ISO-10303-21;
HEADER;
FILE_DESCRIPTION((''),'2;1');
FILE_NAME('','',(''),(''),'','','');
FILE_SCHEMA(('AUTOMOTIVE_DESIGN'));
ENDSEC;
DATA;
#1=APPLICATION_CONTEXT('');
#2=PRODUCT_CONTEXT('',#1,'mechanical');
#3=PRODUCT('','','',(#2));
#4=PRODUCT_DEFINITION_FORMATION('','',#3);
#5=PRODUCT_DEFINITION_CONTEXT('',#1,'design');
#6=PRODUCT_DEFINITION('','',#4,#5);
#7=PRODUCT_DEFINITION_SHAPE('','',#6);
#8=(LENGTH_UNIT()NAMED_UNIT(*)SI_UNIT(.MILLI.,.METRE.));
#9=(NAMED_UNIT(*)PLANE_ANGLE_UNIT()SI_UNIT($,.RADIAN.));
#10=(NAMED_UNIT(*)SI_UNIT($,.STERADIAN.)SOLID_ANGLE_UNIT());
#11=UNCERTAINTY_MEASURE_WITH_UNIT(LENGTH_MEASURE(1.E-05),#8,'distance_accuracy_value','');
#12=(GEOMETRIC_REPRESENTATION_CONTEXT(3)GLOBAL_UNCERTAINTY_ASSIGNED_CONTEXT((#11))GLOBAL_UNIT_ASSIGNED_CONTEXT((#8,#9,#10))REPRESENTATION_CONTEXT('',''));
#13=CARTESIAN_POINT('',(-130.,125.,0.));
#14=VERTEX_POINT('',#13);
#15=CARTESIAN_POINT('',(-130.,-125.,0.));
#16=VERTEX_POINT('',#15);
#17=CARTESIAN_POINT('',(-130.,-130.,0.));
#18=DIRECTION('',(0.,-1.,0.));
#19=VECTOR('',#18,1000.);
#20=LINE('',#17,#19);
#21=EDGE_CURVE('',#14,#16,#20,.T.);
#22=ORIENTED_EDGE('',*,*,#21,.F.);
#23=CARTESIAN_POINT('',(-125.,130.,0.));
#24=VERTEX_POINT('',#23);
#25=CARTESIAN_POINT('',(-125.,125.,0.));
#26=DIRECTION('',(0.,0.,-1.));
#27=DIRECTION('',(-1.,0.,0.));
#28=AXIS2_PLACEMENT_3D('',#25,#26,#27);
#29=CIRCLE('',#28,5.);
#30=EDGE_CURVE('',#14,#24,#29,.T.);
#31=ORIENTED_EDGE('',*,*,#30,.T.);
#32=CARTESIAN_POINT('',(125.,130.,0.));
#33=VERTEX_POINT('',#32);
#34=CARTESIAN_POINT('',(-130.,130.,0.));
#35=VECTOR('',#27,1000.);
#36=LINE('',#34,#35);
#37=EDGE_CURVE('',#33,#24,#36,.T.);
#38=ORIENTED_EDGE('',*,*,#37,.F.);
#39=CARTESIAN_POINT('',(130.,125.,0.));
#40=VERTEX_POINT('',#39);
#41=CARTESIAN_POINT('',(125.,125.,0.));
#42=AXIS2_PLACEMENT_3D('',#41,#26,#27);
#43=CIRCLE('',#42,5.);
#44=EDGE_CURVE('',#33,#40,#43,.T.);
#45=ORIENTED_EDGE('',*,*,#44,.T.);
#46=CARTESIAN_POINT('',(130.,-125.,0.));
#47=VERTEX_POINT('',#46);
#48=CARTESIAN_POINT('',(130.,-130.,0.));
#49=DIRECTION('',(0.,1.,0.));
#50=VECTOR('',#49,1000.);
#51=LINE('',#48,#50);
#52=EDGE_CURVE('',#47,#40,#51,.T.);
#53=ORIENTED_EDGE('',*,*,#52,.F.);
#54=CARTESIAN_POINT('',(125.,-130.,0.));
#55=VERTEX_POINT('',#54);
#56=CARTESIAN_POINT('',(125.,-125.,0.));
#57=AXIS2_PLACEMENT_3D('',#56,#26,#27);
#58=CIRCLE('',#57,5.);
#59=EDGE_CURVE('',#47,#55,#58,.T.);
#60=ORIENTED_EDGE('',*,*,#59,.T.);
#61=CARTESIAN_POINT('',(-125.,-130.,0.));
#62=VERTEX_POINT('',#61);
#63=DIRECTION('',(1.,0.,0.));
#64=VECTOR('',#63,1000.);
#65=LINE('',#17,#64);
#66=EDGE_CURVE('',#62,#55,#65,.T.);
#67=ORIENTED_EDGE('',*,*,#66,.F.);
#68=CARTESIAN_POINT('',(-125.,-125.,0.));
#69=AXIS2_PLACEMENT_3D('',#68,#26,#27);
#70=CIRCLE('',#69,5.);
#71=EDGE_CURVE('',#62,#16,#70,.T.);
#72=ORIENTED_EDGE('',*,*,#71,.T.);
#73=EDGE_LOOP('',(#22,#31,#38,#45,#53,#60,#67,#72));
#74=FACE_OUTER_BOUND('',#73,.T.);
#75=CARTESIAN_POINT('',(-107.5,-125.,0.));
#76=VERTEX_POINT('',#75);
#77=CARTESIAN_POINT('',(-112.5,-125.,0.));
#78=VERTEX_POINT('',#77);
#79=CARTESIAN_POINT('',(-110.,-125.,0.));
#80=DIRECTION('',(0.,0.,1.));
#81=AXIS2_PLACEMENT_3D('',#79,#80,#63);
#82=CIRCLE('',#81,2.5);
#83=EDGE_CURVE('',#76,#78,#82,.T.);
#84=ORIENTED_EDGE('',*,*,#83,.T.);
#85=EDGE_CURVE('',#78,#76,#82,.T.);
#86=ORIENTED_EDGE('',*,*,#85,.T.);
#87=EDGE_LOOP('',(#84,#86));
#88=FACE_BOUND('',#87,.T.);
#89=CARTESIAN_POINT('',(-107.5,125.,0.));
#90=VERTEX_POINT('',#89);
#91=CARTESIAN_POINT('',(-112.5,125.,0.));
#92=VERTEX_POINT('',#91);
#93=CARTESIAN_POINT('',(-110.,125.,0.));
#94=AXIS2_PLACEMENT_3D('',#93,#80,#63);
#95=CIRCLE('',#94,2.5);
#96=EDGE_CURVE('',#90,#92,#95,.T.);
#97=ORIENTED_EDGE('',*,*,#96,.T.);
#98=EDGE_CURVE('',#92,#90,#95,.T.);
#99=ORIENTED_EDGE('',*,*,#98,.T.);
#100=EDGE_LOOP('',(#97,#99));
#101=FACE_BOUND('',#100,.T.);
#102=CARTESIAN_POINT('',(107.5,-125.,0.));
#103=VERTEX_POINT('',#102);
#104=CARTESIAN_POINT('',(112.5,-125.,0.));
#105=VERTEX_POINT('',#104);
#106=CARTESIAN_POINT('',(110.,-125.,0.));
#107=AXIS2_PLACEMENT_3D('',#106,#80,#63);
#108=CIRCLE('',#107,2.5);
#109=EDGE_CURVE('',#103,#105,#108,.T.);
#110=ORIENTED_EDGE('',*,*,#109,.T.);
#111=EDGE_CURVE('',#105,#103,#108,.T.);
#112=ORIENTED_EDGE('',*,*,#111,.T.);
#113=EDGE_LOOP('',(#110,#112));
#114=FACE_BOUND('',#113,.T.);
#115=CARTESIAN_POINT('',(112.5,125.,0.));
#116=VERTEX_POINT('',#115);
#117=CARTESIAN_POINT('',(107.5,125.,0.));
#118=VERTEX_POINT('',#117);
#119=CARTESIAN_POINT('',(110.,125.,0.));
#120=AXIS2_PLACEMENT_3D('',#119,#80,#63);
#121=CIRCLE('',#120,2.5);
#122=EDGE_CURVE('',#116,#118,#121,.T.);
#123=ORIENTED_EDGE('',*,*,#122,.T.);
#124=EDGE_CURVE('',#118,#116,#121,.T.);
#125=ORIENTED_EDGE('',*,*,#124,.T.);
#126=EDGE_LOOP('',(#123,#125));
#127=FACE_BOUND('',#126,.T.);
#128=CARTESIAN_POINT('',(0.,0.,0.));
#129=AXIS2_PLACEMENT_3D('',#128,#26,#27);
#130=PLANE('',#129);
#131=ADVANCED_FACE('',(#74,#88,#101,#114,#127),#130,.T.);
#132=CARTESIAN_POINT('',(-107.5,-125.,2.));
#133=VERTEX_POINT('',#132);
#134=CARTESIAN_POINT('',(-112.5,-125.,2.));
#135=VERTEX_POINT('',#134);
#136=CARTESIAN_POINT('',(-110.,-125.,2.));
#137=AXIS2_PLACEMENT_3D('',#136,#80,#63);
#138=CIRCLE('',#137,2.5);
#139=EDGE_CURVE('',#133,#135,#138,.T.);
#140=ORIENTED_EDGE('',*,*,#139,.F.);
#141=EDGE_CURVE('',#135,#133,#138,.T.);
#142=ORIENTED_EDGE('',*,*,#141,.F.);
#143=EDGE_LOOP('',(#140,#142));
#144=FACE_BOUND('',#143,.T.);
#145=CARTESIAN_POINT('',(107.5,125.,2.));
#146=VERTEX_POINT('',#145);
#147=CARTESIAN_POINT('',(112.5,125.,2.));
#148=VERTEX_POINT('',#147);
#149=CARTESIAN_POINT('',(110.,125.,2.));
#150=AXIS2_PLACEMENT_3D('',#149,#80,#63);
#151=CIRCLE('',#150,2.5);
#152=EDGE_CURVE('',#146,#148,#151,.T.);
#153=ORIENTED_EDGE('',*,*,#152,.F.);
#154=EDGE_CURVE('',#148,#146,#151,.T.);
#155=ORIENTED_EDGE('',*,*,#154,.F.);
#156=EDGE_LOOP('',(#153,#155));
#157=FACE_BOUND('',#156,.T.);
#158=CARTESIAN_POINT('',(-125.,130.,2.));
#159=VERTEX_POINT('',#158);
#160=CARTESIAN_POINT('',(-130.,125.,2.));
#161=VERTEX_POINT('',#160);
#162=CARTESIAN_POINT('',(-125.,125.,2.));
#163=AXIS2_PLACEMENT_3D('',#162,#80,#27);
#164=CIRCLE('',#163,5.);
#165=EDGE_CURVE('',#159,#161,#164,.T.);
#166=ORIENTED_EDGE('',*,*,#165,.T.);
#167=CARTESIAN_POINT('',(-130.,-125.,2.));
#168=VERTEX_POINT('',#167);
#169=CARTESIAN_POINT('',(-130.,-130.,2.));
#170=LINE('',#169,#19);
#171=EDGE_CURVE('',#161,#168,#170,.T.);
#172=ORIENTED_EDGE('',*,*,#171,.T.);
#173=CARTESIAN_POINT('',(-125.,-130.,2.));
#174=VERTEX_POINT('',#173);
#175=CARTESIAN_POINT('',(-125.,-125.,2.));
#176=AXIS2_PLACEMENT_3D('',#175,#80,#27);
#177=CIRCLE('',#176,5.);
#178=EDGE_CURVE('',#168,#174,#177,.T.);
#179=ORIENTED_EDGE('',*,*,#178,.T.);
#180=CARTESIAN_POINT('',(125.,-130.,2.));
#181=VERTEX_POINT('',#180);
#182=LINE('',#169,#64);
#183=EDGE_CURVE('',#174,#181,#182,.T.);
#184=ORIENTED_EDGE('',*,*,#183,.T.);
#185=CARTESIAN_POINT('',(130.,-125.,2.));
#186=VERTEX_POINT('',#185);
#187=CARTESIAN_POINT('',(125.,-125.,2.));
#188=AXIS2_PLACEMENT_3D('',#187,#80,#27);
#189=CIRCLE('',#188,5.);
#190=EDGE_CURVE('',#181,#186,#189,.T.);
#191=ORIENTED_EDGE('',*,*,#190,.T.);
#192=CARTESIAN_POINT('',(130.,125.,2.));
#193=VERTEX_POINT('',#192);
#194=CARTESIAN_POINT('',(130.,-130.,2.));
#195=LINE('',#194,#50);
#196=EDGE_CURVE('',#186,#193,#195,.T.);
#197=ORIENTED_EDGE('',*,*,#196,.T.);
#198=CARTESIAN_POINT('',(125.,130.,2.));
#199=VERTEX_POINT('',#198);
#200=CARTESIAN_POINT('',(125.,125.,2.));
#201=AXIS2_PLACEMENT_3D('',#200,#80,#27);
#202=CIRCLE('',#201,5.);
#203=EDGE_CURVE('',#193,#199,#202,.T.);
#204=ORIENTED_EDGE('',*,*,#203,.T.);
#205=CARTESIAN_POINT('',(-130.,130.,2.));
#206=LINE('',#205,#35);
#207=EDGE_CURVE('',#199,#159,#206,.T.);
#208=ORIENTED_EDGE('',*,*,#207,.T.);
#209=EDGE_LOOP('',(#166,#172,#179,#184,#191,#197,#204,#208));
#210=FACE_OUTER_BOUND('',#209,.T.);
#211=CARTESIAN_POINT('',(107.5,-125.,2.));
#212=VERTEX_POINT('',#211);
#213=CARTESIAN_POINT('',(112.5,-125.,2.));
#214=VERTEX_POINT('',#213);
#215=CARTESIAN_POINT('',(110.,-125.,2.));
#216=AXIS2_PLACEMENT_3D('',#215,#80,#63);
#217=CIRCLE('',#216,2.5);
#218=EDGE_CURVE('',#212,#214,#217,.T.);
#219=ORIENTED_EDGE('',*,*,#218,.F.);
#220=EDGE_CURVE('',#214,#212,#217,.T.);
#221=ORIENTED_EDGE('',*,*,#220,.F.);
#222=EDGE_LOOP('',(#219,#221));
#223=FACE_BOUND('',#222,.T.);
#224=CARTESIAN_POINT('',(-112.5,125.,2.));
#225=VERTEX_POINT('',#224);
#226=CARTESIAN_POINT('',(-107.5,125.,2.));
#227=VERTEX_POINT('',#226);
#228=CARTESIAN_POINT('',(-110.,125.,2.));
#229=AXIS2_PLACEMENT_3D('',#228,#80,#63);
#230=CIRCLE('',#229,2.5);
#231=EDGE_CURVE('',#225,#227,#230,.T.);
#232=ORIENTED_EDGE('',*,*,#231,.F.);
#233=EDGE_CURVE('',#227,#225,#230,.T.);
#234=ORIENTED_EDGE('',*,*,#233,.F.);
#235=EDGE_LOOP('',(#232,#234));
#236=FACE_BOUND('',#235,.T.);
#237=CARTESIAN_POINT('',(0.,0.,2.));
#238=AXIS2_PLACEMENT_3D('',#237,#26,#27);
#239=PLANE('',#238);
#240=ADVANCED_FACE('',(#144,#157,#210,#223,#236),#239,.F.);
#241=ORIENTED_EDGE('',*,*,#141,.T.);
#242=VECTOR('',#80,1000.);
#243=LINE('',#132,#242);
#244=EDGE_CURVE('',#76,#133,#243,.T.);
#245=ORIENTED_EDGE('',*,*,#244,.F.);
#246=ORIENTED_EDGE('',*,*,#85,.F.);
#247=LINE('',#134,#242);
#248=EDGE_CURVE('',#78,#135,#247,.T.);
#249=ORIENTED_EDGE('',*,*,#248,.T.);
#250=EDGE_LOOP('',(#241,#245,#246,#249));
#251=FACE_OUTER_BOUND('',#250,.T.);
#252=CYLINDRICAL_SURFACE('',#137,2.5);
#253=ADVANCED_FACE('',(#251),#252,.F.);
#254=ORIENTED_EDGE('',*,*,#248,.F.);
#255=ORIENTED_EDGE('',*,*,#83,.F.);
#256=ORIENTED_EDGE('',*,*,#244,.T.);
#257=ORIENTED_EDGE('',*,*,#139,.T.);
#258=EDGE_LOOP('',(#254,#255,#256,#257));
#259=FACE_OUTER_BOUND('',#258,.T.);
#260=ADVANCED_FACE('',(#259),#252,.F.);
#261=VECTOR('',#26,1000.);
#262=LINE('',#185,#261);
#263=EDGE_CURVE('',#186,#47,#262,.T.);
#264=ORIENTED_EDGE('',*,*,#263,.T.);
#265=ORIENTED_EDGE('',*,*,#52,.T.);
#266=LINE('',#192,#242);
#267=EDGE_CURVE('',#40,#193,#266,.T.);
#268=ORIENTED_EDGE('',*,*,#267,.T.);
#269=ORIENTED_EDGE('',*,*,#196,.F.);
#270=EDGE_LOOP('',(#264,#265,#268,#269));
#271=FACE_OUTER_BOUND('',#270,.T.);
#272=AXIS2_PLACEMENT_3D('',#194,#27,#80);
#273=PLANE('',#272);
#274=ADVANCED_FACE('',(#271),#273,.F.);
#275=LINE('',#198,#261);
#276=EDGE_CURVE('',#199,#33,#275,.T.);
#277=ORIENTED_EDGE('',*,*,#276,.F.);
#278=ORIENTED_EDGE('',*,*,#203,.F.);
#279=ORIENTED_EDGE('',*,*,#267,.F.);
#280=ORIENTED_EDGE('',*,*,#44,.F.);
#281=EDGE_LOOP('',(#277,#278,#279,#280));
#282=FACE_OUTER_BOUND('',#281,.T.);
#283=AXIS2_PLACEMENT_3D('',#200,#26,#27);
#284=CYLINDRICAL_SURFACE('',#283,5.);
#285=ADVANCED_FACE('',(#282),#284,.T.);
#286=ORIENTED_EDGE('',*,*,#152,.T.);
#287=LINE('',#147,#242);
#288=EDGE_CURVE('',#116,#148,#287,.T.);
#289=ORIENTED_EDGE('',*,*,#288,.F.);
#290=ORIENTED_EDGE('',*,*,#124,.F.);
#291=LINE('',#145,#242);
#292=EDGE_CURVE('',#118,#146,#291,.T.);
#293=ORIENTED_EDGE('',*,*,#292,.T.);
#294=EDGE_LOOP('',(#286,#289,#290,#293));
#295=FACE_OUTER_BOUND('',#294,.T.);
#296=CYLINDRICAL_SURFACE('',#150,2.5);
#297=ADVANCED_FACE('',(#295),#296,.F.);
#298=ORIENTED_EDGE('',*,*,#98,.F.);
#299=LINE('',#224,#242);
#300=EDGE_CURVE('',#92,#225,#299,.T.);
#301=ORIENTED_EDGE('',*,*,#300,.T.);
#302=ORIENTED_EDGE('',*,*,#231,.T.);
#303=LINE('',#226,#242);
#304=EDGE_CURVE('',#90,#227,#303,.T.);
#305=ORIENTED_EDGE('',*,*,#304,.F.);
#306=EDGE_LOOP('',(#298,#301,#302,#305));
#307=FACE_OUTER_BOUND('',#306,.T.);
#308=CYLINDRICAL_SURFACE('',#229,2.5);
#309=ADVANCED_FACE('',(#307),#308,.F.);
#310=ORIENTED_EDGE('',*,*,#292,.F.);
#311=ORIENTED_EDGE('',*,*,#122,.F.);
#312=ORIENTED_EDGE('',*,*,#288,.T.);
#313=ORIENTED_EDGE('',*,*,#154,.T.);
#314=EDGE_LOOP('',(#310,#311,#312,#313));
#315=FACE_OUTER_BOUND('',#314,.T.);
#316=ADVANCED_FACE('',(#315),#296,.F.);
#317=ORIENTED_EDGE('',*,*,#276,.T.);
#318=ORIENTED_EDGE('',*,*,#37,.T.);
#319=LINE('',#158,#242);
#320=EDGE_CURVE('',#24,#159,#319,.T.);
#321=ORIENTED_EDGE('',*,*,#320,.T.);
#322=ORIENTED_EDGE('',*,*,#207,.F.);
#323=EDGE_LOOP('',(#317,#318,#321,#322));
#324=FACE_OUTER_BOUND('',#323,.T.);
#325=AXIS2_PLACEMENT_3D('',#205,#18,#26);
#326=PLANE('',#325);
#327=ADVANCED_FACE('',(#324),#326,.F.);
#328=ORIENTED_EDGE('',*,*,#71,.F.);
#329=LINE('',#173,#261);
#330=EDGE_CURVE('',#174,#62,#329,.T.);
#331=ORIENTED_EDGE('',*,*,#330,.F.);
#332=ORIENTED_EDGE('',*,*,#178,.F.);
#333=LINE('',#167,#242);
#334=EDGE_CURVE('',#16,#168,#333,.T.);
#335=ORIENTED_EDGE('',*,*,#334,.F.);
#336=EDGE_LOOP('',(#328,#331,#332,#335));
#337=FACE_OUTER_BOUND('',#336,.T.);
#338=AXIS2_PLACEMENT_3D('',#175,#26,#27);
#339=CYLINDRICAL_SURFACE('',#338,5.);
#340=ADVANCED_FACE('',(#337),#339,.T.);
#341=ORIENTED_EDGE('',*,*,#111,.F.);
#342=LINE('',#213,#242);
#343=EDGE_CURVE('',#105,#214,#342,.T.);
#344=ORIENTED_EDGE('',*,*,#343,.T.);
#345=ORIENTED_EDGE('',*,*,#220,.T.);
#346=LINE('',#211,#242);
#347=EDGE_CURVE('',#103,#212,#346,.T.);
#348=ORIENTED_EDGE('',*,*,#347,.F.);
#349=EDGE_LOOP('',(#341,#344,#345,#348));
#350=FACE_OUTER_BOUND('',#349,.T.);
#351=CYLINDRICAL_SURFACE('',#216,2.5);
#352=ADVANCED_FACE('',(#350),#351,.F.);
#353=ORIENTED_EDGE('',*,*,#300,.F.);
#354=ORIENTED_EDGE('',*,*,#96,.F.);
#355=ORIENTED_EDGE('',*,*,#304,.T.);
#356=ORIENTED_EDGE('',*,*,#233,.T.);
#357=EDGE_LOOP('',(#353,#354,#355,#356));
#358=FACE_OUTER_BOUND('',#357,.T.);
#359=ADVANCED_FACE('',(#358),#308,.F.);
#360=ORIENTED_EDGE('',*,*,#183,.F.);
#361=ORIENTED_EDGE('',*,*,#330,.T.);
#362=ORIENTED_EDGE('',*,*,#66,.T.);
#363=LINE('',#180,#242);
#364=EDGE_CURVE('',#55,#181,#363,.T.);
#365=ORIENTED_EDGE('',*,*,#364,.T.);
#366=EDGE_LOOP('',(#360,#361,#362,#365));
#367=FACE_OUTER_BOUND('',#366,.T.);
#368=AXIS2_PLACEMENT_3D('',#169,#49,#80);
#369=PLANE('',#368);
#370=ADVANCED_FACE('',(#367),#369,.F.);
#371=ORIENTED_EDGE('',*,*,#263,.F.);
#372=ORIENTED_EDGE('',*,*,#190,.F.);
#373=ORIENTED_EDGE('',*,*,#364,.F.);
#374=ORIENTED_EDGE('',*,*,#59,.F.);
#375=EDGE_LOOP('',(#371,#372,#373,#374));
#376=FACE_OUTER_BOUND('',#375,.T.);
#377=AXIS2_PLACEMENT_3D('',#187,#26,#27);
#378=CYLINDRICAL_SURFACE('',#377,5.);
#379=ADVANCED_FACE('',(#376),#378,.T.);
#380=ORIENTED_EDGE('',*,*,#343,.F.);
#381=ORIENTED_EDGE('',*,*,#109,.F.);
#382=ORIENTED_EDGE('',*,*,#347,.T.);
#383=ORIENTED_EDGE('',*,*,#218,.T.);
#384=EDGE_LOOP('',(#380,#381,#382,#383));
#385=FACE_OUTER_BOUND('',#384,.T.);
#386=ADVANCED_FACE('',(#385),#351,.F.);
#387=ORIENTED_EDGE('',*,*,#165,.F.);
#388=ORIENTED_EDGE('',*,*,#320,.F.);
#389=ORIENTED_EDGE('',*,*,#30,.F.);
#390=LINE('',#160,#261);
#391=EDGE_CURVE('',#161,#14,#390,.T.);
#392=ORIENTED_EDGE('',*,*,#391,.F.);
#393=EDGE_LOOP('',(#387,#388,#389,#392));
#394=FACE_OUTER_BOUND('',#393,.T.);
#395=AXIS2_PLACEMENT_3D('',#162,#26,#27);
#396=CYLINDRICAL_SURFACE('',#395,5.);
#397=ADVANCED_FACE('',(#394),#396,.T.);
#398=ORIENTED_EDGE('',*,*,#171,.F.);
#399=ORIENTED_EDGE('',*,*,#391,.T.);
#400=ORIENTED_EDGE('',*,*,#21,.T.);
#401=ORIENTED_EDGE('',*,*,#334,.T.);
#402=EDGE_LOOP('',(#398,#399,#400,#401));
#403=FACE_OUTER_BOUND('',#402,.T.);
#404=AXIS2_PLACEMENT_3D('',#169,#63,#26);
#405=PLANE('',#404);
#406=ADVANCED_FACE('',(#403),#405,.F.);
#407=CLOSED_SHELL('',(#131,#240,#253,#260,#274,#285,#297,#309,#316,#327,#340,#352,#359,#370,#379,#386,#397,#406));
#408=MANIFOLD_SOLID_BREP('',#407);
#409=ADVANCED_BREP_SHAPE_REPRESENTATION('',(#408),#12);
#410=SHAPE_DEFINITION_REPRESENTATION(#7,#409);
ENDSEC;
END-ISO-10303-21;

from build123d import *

# Parameters (mm, degrees)
SKETCH_1_W            = 260
SKETCH_1_H            = 260
EXTRUDE_1_DEPTH       = 2
FILLET_1_R            = 5
HOLE_WIZARD_5_0_5_1_D = 5


with BuildPart() as part:
    # 草图1 → 凸台-拉伸1 (new body)
    with BuildSketch(Plane.XY):
        Rectangle(SKETCH_1_W, SKETCH_1_H)
    extrude(amount=EXTRUDE_1_DEPTH)

    # 圆角1
    fillet_1_edges = [part.edges().sort_by_distance(p)[0] for p in [
        (130, -130, 1),
        (-130, -130, 1),
        (-130, 130, 1),
        (130, 130, 1),
    ]]
    fillet(fillet_1_edges, radius=FILLET_1_R)

    # Ø5.0 (5) 直径孔1 (through all)
    with Locations(Plane.XY.offset(2)):
        with Locations((-110, 125), (-110, -125), (110, -125), (110, 125)):
            Hole(HOLE_WIZARD_5_0_5_1_D / 2)


solid = part.part
